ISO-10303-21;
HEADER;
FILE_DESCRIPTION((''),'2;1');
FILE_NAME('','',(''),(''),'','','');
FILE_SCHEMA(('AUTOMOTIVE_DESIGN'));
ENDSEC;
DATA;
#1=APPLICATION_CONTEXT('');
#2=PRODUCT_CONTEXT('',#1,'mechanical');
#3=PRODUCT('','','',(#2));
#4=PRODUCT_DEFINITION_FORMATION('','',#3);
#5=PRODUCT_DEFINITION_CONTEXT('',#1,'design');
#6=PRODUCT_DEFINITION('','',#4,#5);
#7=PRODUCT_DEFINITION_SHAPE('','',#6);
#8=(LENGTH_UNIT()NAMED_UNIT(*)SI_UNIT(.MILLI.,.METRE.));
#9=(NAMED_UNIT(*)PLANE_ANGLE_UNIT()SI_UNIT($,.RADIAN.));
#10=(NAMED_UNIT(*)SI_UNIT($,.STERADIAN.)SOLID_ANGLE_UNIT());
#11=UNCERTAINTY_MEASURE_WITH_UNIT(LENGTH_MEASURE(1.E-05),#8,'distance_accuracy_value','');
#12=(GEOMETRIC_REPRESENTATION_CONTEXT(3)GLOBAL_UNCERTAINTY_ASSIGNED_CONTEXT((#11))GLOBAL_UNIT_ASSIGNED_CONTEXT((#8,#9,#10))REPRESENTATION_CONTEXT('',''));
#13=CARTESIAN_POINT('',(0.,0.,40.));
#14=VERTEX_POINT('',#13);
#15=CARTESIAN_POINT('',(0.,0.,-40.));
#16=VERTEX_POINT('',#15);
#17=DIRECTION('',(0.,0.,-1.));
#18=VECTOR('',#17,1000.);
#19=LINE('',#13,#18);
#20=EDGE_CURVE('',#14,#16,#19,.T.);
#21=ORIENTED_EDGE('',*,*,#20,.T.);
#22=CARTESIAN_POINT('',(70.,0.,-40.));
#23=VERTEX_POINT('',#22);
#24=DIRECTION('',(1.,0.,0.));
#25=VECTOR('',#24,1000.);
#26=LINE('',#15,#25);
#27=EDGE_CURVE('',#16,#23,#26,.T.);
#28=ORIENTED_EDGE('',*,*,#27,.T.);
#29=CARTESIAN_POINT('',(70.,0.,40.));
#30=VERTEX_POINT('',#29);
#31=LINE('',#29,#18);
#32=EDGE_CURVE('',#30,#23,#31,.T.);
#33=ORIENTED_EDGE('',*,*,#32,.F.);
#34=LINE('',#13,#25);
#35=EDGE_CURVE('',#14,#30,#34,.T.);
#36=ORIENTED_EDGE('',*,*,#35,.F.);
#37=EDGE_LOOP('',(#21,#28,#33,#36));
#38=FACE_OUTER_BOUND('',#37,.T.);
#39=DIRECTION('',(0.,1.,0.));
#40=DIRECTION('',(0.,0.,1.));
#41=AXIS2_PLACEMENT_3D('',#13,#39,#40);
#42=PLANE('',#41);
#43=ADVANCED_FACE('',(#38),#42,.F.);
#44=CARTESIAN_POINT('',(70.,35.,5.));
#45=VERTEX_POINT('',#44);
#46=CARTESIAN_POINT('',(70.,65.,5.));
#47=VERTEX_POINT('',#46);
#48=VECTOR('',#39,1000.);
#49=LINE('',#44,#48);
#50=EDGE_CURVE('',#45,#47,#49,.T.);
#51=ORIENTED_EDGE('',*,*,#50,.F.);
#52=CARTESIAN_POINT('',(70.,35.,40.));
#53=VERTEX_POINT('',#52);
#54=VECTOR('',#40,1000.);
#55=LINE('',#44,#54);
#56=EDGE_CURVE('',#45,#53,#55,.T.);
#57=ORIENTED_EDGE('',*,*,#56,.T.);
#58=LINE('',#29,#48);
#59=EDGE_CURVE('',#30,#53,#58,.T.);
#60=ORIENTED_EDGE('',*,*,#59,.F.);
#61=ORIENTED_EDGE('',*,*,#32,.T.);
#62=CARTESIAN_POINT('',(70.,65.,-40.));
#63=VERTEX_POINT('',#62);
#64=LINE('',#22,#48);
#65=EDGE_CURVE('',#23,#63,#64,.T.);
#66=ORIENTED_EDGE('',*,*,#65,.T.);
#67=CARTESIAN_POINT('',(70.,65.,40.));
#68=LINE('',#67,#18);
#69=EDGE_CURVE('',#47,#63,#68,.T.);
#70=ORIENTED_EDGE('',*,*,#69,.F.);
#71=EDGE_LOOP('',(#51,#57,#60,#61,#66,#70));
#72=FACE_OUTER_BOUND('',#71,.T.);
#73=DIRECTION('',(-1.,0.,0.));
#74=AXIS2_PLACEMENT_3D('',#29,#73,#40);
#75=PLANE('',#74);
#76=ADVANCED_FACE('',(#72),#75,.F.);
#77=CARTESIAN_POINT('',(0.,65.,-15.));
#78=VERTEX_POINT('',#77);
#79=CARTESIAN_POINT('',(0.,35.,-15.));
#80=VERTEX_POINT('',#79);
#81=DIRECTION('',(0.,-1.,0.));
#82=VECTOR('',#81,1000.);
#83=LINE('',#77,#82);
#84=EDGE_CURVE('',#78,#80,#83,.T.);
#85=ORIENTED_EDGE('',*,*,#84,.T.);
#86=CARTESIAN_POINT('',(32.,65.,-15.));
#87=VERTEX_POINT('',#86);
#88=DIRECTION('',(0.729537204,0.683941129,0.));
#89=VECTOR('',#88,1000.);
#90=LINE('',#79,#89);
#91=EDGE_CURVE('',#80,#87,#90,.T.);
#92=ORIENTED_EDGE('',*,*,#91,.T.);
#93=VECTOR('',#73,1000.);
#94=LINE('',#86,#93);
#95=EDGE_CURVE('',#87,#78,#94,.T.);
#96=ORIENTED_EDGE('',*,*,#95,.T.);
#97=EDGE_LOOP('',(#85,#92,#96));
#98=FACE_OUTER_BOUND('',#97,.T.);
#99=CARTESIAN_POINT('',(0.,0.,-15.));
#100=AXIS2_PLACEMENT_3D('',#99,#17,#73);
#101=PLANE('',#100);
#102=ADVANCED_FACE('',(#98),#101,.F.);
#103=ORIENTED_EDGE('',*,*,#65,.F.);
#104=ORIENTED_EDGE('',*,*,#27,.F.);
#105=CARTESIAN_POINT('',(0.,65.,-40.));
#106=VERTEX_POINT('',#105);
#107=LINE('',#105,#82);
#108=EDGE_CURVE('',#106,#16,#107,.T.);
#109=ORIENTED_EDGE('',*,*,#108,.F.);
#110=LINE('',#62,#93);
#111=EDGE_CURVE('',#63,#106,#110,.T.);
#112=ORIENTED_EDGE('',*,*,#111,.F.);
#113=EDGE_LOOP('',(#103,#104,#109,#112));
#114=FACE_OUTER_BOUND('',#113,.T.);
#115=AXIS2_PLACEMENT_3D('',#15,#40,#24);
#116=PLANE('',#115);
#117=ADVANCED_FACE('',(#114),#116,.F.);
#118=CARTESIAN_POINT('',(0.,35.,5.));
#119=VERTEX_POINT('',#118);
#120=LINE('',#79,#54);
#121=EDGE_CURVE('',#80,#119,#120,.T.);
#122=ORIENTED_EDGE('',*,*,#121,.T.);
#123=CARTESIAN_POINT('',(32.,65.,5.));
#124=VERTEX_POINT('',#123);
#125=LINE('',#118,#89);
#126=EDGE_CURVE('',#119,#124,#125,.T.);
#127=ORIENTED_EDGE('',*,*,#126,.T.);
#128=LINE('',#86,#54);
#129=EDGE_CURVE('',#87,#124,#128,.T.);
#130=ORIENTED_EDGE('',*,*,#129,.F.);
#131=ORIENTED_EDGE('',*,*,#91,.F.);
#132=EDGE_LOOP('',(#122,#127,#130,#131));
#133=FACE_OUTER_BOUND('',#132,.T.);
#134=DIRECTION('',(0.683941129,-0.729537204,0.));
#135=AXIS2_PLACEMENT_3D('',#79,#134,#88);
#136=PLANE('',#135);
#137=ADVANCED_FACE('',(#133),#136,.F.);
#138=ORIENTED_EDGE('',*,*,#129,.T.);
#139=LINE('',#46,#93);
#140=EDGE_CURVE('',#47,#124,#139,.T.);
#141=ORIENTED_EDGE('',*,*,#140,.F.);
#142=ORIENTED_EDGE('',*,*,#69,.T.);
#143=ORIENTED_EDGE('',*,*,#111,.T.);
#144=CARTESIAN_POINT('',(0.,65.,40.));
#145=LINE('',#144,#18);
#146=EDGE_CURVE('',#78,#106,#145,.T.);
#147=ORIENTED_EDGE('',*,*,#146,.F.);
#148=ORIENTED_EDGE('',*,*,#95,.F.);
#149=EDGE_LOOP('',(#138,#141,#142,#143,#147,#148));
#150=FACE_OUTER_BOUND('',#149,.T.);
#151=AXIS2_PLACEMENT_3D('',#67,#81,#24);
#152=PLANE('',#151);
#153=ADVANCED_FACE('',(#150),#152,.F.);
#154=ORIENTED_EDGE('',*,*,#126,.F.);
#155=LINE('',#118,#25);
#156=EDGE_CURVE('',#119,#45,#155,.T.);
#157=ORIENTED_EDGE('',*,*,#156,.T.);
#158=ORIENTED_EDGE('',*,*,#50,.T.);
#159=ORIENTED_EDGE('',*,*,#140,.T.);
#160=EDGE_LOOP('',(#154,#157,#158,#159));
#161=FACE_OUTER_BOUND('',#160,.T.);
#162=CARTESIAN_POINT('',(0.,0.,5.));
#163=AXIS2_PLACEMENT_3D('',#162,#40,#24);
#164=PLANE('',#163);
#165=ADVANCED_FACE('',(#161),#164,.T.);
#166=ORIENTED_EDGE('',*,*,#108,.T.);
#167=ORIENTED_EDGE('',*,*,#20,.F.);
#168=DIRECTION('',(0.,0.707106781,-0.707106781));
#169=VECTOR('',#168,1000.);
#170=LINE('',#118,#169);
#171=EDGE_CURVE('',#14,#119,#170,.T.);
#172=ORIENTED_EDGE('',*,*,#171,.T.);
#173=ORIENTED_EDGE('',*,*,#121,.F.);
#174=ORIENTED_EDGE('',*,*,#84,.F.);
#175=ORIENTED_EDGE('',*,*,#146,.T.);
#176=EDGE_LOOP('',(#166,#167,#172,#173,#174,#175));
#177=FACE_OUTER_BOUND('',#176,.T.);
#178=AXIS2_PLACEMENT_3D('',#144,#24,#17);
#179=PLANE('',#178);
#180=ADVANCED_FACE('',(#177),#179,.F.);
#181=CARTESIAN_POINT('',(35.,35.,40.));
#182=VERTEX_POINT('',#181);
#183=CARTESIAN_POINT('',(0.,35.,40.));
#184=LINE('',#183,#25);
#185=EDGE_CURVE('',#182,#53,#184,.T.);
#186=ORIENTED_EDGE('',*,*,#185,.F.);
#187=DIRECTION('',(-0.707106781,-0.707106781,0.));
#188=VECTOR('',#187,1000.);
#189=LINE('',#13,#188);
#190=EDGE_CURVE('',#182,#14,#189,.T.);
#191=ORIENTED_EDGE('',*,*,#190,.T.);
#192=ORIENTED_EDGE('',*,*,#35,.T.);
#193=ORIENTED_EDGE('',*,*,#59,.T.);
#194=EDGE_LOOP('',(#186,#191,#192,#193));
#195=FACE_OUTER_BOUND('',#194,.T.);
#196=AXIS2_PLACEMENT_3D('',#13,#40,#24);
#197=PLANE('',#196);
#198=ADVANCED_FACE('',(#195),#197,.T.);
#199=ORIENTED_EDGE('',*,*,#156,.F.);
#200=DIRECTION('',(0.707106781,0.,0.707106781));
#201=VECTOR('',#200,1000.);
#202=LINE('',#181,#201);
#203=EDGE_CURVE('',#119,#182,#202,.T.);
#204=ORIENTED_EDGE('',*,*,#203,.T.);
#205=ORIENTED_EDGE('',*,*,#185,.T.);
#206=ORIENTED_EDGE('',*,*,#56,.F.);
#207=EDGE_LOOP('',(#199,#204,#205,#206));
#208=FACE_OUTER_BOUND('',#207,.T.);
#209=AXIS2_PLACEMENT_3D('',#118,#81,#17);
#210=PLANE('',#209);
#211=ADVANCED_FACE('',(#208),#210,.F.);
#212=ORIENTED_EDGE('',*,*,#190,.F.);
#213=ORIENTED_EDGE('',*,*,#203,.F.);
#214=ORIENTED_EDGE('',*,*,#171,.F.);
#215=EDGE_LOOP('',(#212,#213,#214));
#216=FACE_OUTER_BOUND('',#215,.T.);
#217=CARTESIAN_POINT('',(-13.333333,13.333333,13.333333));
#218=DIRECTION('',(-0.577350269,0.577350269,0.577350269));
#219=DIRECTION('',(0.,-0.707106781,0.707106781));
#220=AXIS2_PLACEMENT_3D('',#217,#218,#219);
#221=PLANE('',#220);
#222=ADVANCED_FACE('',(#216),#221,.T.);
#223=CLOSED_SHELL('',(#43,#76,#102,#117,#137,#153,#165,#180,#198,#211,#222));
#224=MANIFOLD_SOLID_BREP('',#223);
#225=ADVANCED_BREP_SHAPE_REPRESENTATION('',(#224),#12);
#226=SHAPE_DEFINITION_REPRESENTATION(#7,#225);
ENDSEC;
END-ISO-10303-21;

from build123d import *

# Parameters (mm, degrees)
BLOCK_PROFILE_SKETCH_70X65_W = 70
BLOCK_PROFILE_SKETCH_70X65_H = 65
BASE_BLOCK_70X65X80_DEPTH    = 40
UPPER_STEP_SKETCH_W          = 70
UPPER_STEP_SKETCH_H          = 30
UPPER_STEP_CUT_35_DEPTH      = 35
LOWER_STEP_CUT_20_DEPTH      = 20
ANGLED_CORNER_CUT_DEPTH      = 56


with BuildPart() as part:
    # Block Profile Sketch 70x65 → Base Block 70x65x80 (new, symmetric)
    with BuildSketch(Plane.XY):
        with Locations((35, 32.5)):
            Rectangle(BLOCK_PROFILE_SKETCH_70X65_W, BLOCK_PROFILE_SKETCH_70X65_H)
    extrude(amount=BASE_BLOCK_70X65X80_DEPTH, both=True)

    # Upper Step Sketch → Upper Step Cut 35 (cut)
    with BuildSketch(Plane.XY.offset(40)):
        with Locations((35, 50)):
            Rectangle(UPPER_STEP_SKETCH_W, UPPER_STEP_SKETCH_H)
    extrude(amount=-UPPER_STEP_CUT_35_DEPTH, mode=Mode.SUBTRACT)

    # Lower Step Sketch → Lower Step Cut 20 (cut)
    with BuildSketch(Plane.XY.offset(5)):
        Polygon((0, 35), (32, 65), (0, 65), align=None)
    extrude(amount=-LOWER_STEP_CUT_20_DEPTH, mode=Mode.SUBTRACT)

    # Corner Cut Sketch → Angled Corner Cut (cut)
    with BuildSketch(Plane(origin=(-13.333333333, 13.333333333, 13.333333333), x_dir=(-0.8164965809277261, -0.408248290463863, -0.408248290463863), z_dir=(0.5773502691896257, -0.5773502691896258, -0.5773502691896258))):
        Polygon((-16.329931619, 21.213203436), (-16.329931619, -28.284271247), (-59.196002117, -3.535533906), align=None)
    extrude(amount=-ANGLED_CORNER_CUT_DEPTH, mode=Mode.SUBTRACT)


solid = part.part
